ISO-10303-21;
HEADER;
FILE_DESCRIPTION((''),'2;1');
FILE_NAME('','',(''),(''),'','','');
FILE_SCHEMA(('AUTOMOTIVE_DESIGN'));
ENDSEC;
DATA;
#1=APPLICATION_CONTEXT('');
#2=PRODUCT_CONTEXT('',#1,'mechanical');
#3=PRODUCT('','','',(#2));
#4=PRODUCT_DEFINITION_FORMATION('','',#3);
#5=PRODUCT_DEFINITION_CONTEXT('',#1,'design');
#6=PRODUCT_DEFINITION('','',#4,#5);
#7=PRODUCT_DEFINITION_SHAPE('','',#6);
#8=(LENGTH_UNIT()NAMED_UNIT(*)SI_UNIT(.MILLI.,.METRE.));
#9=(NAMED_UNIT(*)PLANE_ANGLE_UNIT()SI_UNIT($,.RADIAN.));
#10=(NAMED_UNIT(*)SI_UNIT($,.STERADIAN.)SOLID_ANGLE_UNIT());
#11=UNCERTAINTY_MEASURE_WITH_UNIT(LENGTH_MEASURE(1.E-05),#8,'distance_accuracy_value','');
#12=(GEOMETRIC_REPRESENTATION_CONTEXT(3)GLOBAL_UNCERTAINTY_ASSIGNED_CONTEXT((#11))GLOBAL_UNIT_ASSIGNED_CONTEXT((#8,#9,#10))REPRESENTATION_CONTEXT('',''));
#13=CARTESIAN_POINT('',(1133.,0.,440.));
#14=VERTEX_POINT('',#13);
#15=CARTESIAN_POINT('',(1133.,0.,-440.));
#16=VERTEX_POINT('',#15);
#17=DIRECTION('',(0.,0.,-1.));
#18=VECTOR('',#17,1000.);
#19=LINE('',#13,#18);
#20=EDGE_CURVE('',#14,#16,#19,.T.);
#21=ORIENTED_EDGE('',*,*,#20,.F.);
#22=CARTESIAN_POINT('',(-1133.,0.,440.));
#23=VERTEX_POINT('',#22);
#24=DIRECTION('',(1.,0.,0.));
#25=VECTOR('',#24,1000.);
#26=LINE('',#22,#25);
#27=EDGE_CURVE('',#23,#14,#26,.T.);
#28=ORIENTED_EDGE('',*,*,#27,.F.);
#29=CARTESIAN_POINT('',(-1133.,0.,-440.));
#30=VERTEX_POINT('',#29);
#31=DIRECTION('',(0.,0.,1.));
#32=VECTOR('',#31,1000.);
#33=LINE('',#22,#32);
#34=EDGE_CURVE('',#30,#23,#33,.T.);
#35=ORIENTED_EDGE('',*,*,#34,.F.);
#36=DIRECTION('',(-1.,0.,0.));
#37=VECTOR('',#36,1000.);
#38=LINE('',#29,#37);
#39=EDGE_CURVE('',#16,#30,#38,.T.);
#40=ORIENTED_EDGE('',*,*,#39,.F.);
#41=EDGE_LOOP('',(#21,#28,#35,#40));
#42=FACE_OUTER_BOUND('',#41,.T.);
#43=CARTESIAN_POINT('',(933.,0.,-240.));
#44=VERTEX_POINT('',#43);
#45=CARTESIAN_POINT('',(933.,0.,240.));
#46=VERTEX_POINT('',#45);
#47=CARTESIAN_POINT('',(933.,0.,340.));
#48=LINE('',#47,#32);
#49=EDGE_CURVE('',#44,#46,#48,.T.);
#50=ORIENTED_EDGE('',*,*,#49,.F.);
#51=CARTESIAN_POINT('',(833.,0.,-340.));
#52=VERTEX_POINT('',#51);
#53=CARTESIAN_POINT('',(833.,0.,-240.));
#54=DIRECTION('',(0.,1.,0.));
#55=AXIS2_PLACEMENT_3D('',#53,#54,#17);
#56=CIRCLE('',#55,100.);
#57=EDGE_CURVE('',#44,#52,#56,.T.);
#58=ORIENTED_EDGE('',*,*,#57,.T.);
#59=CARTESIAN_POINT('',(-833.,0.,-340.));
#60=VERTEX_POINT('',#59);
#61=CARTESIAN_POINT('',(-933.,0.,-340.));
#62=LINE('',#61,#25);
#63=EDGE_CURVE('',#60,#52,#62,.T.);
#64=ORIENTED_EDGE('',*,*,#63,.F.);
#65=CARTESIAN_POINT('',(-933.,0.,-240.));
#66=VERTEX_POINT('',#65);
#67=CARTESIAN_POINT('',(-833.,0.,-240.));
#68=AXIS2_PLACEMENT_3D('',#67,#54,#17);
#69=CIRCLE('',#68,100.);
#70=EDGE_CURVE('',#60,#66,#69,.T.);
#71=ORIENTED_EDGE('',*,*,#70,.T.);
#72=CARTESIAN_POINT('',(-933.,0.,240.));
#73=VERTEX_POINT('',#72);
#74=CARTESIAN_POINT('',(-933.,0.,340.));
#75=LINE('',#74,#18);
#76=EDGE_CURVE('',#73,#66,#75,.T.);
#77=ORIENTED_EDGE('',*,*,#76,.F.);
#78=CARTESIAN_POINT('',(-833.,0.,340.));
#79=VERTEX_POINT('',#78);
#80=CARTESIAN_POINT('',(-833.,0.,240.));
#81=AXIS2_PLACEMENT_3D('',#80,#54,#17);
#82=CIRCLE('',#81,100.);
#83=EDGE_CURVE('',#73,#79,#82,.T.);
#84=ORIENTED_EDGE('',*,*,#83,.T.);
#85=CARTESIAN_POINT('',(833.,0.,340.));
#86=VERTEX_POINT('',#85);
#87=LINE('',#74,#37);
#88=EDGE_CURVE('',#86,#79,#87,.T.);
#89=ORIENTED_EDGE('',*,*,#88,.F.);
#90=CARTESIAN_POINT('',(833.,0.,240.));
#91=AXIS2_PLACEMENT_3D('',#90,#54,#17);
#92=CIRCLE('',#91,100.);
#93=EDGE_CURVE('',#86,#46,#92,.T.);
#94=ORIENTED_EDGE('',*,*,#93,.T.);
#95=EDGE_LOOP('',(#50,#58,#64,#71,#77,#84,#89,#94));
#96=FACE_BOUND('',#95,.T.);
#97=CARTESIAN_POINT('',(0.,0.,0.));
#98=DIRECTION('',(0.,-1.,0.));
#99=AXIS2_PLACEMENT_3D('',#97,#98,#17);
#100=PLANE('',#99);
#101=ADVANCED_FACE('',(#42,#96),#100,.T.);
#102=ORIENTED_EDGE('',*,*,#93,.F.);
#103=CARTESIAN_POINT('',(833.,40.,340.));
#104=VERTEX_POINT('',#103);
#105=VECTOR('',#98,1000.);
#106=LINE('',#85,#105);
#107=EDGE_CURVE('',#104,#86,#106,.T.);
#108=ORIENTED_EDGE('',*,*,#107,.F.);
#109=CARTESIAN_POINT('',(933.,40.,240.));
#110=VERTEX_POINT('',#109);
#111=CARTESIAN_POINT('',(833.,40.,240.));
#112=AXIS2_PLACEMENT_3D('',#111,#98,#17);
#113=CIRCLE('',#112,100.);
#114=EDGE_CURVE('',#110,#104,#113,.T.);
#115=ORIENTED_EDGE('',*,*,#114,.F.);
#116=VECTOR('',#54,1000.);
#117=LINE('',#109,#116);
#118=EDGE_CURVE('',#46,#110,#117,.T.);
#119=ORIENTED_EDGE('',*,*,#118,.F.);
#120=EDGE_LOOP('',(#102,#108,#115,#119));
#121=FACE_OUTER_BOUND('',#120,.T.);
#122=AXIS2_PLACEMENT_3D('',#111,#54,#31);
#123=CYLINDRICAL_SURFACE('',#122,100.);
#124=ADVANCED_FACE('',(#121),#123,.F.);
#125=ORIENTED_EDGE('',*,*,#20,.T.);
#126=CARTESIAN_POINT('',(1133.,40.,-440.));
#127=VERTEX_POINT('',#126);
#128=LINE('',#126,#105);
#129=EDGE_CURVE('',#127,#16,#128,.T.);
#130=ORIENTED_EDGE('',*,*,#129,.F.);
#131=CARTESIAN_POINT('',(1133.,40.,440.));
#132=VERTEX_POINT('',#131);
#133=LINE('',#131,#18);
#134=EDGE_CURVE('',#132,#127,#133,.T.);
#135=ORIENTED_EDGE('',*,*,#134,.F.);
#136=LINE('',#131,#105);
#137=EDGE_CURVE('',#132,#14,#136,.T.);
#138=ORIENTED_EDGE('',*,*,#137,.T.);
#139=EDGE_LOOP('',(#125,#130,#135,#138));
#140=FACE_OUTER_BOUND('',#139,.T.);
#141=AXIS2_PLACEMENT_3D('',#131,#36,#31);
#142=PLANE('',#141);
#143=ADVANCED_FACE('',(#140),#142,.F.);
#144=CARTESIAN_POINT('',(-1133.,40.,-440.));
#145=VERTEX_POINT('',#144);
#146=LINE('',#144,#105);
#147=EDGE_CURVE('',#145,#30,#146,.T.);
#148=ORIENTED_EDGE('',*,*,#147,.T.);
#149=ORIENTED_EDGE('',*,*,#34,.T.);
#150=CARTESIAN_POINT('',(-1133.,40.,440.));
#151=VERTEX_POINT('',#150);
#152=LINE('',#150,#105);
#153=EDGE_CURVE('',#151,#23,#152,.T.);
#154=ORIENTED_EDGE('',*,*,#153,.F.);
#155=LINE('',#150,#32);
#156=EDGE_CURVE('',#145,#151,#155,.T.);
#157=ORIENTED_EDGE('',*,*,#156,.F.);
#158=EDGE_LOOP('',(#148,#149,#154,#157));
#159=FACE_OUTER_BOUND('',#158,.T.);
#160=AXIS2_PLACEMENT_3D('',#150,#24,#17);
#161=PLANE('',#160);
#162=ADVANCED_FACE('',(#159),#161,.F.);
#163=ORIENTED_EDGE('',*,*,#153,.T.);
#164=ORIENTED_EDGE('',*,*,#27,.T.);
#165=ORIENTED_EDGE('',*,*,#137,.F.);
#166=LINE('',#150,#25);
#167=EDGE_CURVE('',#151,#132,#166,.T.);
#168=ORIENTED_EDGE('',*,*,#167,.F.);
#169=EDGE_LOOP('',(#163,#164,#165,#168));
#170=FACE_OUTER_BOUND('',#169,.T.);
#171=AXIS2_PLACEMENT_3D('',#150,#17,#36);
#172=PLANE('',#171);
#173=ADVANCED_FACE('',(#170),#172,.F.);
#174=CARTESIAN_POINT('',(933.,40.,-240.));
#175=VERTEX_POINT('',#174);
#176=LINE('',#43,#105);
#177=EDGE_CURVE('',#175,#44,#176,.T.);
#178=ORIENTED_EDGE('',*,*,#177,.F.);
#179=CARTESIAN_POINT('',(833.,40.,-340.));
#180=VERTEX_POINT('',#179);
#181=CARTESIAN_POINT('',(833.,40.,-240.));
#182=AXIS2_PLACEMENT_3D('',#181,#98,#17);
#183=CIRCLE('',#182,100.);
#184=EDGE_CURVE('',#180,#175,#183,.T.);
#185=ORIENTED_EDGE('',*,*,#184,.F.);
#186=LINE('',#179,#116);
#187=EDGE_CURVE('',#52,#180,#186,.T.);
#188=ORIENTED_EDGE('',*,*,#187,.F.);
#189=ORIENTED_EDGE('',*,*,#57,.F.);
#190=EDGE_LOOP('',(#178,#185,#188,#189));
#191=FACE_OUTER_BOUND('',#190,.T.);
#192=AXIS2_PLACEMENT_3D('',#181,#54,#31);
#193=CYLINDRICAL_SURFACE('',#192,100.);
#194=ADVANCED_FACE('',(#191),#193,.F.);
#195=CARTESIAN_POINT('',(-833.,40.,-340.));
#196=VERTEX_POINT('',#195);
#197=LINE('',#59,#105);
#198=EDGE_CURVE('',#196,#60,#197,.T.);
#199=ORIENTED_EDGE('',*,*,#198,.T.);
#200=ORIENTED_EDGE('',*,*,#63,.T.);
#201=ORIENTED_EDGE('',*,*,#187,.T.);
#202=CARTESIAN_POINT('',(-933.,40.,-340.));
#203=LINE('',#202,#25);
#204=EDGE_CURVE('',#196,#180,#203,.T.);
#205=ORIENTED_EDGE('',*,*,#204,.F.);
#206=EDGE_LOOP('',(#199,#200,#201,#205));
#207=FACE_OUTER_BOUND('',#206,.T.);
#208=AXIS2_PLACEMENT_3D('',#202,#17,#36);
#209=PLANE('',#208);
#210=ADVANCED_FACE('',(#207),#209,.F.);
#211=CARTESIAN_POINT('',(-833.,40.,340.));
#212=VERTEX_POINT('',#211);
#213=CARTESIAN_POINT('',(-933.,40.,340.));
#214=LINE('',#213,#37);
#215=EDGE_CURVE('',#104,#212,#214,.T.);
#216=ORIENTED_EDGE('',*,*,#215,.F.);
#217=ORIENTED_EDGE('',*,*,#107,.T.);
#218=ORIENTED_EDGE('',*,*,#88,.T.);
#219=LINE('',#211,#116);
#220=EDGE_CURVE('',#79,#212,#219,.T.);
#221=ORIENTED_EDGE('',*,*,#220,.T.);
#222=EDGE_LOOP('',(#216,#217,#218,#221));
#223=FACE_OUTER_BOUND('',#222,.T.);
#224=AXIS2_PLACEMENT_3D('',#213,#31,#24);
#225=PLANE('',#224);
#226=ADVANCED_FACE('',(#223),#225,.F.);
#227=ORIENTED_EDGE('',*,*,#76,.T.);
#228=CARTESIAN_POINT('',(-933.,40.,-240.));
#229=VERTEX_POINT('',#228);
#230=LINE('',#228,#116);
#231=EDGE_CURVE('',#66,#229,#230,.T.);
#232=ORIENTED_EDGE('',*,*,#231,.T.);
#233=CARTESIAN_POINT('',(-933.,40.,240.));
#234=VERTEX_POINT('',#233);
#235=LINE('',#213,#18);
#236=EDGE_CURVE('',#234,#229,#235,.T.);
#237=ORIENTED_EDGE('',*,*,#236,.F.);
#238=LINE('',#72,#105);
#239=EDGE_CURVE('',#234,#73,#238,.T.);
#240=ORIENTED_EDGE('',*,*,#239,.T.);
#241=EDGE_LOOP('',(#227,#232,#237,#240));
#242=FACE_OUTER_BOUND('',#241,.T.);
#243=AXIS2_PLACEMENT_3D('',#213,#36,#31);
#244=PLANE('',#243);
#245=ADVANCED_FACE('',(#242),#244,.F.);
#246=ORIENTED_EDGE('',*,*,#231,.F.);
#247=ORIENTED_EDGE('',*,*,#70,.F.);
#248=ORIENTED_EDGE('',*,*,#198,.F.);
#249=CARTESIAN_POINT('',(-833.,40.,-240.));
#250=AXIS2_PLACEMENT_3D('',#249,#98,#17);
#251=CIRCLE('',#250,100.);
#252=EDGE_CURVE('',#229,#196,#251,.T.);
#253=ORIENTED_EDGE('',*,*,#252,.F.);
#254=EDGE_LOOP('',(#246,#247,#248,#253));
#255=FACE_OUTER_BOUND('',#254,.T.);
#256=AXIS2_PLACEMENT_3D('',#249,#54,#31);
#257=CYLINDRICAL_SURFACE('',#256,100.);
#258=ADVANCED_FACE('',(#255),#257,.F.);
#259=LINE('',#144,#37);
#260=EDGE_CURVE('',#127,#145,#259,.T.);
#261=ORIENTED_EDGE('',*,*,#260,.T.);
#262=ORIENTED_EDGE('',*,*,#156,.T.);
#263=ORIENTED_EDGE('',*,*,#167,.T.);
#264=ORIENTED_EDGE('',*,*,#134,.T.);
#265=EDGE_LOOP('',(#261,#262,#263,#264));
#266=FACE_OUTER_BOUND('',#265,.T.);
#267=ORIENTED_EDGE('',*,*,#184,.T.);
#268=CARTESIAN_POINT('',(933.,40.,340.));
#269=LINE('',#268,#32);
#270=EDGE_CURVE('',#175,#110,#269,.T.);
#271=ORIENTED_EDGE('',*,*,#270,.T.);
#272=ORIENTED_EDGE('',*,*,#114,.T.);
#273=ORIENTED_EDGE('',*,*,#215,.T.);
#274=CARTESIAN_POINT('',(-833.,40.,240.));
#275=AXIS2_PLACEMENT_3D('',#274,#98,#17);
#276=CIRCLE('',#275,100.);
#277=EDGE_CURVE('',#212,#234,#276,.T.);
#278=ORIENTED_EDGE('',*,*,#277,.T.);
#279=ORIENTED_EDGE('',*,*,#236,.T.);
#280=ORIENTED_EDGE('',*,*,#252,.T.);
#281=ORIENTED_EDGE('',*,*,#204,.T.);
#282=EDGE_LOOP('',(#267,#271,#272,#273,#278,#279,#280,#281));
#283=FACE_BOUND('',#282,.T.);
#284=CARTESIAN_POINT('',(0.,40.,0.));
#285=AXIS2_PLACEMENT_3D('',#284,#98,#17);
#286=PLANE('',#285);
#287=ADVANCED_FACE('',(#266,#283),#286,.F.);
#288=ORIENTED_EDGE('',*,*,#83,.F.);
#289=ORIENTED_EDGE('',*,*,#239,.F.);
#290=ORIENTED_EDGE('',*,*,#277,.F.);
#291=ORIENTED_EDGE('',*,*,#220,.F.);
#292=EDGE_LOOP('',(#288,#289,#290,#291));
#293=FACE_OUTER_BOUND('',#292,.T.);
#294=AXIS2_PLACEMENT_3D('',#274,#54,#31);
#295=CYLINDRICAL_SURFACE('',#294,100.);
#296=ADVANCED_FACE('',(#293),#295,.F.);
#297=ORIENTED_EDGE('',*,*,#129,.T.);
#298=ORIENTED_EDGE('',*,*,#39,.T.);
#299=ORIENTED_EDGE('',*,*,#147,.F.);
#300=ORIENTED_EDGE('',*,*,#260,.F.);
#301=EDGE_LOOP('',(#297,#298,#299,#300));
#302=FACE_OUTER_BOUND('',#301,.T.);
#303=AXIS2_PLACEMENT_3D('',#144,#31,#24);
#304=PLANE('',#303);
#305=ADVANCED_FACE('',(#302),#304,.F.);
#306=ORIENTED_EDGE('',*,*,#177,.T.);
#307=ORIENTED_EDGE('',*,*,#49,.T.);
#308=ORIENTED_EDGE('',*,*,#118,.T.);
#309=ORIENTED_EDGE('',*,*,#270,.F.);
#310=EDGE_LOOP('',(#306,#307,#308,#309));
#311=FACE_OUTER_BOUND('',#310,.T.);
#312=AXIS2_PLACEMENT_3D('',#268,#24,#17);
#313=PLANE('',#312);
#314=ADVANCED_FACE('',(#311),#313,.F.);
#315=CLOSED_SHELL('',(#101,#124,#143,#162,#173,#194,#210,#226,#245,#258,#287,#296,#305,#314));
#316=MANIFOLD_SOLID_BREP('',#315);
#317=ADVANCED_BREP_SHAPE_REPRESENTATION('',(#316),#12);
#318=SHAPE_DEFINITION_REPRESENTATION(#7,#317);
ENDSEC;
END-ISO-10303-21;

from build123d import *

# Parameters (mm, degrees)
SKETCH_1_W          = 2266
SKETCH_1_H          = 880
EXTRUDE_1_DEPTH     = 40
SKETCH_2_W          = 1866
SKETCH_2_H          = 680
CUT_EXTRUDE_1_DEPTH = 1217.095802147
FILLET_1_R          = 100


with BuildPart() as part:
    # 草图1 → 凸台-拉伸1 (new body)
    with BuildSketch(Plane(origin=(0, 0, 0), x_dir=(1, 0, 0), z_dir=(0, 1, 0))):
        Rectangle(SKETCH_1_W, SKETCH_1_H)
    extrude(amount=EXTRUDE_1_DEPTH)

    # 草图2 → 切除-拉伸1 (cut, through all)
    with BuildSketch(Plane.XZ):
        Rectangle(SKETCH_2_W, SKETCH_2_H)
    extrude(amount=-CUT_EXTRUDE_1_DEPTH, mode=Mode.SUBTRACT)

    # 圆角1
    fillet_1_edges = [part.edges().sort_by_distance(p)[0] for p in [
        (933, 20, 340),
        (933, 20, -340),
        (-933, 20, -340),
        (-933, 20, 340),
    ]]
    fillet(fillet_1_edges, radius=FILLET_1_R)


solid = part.part
